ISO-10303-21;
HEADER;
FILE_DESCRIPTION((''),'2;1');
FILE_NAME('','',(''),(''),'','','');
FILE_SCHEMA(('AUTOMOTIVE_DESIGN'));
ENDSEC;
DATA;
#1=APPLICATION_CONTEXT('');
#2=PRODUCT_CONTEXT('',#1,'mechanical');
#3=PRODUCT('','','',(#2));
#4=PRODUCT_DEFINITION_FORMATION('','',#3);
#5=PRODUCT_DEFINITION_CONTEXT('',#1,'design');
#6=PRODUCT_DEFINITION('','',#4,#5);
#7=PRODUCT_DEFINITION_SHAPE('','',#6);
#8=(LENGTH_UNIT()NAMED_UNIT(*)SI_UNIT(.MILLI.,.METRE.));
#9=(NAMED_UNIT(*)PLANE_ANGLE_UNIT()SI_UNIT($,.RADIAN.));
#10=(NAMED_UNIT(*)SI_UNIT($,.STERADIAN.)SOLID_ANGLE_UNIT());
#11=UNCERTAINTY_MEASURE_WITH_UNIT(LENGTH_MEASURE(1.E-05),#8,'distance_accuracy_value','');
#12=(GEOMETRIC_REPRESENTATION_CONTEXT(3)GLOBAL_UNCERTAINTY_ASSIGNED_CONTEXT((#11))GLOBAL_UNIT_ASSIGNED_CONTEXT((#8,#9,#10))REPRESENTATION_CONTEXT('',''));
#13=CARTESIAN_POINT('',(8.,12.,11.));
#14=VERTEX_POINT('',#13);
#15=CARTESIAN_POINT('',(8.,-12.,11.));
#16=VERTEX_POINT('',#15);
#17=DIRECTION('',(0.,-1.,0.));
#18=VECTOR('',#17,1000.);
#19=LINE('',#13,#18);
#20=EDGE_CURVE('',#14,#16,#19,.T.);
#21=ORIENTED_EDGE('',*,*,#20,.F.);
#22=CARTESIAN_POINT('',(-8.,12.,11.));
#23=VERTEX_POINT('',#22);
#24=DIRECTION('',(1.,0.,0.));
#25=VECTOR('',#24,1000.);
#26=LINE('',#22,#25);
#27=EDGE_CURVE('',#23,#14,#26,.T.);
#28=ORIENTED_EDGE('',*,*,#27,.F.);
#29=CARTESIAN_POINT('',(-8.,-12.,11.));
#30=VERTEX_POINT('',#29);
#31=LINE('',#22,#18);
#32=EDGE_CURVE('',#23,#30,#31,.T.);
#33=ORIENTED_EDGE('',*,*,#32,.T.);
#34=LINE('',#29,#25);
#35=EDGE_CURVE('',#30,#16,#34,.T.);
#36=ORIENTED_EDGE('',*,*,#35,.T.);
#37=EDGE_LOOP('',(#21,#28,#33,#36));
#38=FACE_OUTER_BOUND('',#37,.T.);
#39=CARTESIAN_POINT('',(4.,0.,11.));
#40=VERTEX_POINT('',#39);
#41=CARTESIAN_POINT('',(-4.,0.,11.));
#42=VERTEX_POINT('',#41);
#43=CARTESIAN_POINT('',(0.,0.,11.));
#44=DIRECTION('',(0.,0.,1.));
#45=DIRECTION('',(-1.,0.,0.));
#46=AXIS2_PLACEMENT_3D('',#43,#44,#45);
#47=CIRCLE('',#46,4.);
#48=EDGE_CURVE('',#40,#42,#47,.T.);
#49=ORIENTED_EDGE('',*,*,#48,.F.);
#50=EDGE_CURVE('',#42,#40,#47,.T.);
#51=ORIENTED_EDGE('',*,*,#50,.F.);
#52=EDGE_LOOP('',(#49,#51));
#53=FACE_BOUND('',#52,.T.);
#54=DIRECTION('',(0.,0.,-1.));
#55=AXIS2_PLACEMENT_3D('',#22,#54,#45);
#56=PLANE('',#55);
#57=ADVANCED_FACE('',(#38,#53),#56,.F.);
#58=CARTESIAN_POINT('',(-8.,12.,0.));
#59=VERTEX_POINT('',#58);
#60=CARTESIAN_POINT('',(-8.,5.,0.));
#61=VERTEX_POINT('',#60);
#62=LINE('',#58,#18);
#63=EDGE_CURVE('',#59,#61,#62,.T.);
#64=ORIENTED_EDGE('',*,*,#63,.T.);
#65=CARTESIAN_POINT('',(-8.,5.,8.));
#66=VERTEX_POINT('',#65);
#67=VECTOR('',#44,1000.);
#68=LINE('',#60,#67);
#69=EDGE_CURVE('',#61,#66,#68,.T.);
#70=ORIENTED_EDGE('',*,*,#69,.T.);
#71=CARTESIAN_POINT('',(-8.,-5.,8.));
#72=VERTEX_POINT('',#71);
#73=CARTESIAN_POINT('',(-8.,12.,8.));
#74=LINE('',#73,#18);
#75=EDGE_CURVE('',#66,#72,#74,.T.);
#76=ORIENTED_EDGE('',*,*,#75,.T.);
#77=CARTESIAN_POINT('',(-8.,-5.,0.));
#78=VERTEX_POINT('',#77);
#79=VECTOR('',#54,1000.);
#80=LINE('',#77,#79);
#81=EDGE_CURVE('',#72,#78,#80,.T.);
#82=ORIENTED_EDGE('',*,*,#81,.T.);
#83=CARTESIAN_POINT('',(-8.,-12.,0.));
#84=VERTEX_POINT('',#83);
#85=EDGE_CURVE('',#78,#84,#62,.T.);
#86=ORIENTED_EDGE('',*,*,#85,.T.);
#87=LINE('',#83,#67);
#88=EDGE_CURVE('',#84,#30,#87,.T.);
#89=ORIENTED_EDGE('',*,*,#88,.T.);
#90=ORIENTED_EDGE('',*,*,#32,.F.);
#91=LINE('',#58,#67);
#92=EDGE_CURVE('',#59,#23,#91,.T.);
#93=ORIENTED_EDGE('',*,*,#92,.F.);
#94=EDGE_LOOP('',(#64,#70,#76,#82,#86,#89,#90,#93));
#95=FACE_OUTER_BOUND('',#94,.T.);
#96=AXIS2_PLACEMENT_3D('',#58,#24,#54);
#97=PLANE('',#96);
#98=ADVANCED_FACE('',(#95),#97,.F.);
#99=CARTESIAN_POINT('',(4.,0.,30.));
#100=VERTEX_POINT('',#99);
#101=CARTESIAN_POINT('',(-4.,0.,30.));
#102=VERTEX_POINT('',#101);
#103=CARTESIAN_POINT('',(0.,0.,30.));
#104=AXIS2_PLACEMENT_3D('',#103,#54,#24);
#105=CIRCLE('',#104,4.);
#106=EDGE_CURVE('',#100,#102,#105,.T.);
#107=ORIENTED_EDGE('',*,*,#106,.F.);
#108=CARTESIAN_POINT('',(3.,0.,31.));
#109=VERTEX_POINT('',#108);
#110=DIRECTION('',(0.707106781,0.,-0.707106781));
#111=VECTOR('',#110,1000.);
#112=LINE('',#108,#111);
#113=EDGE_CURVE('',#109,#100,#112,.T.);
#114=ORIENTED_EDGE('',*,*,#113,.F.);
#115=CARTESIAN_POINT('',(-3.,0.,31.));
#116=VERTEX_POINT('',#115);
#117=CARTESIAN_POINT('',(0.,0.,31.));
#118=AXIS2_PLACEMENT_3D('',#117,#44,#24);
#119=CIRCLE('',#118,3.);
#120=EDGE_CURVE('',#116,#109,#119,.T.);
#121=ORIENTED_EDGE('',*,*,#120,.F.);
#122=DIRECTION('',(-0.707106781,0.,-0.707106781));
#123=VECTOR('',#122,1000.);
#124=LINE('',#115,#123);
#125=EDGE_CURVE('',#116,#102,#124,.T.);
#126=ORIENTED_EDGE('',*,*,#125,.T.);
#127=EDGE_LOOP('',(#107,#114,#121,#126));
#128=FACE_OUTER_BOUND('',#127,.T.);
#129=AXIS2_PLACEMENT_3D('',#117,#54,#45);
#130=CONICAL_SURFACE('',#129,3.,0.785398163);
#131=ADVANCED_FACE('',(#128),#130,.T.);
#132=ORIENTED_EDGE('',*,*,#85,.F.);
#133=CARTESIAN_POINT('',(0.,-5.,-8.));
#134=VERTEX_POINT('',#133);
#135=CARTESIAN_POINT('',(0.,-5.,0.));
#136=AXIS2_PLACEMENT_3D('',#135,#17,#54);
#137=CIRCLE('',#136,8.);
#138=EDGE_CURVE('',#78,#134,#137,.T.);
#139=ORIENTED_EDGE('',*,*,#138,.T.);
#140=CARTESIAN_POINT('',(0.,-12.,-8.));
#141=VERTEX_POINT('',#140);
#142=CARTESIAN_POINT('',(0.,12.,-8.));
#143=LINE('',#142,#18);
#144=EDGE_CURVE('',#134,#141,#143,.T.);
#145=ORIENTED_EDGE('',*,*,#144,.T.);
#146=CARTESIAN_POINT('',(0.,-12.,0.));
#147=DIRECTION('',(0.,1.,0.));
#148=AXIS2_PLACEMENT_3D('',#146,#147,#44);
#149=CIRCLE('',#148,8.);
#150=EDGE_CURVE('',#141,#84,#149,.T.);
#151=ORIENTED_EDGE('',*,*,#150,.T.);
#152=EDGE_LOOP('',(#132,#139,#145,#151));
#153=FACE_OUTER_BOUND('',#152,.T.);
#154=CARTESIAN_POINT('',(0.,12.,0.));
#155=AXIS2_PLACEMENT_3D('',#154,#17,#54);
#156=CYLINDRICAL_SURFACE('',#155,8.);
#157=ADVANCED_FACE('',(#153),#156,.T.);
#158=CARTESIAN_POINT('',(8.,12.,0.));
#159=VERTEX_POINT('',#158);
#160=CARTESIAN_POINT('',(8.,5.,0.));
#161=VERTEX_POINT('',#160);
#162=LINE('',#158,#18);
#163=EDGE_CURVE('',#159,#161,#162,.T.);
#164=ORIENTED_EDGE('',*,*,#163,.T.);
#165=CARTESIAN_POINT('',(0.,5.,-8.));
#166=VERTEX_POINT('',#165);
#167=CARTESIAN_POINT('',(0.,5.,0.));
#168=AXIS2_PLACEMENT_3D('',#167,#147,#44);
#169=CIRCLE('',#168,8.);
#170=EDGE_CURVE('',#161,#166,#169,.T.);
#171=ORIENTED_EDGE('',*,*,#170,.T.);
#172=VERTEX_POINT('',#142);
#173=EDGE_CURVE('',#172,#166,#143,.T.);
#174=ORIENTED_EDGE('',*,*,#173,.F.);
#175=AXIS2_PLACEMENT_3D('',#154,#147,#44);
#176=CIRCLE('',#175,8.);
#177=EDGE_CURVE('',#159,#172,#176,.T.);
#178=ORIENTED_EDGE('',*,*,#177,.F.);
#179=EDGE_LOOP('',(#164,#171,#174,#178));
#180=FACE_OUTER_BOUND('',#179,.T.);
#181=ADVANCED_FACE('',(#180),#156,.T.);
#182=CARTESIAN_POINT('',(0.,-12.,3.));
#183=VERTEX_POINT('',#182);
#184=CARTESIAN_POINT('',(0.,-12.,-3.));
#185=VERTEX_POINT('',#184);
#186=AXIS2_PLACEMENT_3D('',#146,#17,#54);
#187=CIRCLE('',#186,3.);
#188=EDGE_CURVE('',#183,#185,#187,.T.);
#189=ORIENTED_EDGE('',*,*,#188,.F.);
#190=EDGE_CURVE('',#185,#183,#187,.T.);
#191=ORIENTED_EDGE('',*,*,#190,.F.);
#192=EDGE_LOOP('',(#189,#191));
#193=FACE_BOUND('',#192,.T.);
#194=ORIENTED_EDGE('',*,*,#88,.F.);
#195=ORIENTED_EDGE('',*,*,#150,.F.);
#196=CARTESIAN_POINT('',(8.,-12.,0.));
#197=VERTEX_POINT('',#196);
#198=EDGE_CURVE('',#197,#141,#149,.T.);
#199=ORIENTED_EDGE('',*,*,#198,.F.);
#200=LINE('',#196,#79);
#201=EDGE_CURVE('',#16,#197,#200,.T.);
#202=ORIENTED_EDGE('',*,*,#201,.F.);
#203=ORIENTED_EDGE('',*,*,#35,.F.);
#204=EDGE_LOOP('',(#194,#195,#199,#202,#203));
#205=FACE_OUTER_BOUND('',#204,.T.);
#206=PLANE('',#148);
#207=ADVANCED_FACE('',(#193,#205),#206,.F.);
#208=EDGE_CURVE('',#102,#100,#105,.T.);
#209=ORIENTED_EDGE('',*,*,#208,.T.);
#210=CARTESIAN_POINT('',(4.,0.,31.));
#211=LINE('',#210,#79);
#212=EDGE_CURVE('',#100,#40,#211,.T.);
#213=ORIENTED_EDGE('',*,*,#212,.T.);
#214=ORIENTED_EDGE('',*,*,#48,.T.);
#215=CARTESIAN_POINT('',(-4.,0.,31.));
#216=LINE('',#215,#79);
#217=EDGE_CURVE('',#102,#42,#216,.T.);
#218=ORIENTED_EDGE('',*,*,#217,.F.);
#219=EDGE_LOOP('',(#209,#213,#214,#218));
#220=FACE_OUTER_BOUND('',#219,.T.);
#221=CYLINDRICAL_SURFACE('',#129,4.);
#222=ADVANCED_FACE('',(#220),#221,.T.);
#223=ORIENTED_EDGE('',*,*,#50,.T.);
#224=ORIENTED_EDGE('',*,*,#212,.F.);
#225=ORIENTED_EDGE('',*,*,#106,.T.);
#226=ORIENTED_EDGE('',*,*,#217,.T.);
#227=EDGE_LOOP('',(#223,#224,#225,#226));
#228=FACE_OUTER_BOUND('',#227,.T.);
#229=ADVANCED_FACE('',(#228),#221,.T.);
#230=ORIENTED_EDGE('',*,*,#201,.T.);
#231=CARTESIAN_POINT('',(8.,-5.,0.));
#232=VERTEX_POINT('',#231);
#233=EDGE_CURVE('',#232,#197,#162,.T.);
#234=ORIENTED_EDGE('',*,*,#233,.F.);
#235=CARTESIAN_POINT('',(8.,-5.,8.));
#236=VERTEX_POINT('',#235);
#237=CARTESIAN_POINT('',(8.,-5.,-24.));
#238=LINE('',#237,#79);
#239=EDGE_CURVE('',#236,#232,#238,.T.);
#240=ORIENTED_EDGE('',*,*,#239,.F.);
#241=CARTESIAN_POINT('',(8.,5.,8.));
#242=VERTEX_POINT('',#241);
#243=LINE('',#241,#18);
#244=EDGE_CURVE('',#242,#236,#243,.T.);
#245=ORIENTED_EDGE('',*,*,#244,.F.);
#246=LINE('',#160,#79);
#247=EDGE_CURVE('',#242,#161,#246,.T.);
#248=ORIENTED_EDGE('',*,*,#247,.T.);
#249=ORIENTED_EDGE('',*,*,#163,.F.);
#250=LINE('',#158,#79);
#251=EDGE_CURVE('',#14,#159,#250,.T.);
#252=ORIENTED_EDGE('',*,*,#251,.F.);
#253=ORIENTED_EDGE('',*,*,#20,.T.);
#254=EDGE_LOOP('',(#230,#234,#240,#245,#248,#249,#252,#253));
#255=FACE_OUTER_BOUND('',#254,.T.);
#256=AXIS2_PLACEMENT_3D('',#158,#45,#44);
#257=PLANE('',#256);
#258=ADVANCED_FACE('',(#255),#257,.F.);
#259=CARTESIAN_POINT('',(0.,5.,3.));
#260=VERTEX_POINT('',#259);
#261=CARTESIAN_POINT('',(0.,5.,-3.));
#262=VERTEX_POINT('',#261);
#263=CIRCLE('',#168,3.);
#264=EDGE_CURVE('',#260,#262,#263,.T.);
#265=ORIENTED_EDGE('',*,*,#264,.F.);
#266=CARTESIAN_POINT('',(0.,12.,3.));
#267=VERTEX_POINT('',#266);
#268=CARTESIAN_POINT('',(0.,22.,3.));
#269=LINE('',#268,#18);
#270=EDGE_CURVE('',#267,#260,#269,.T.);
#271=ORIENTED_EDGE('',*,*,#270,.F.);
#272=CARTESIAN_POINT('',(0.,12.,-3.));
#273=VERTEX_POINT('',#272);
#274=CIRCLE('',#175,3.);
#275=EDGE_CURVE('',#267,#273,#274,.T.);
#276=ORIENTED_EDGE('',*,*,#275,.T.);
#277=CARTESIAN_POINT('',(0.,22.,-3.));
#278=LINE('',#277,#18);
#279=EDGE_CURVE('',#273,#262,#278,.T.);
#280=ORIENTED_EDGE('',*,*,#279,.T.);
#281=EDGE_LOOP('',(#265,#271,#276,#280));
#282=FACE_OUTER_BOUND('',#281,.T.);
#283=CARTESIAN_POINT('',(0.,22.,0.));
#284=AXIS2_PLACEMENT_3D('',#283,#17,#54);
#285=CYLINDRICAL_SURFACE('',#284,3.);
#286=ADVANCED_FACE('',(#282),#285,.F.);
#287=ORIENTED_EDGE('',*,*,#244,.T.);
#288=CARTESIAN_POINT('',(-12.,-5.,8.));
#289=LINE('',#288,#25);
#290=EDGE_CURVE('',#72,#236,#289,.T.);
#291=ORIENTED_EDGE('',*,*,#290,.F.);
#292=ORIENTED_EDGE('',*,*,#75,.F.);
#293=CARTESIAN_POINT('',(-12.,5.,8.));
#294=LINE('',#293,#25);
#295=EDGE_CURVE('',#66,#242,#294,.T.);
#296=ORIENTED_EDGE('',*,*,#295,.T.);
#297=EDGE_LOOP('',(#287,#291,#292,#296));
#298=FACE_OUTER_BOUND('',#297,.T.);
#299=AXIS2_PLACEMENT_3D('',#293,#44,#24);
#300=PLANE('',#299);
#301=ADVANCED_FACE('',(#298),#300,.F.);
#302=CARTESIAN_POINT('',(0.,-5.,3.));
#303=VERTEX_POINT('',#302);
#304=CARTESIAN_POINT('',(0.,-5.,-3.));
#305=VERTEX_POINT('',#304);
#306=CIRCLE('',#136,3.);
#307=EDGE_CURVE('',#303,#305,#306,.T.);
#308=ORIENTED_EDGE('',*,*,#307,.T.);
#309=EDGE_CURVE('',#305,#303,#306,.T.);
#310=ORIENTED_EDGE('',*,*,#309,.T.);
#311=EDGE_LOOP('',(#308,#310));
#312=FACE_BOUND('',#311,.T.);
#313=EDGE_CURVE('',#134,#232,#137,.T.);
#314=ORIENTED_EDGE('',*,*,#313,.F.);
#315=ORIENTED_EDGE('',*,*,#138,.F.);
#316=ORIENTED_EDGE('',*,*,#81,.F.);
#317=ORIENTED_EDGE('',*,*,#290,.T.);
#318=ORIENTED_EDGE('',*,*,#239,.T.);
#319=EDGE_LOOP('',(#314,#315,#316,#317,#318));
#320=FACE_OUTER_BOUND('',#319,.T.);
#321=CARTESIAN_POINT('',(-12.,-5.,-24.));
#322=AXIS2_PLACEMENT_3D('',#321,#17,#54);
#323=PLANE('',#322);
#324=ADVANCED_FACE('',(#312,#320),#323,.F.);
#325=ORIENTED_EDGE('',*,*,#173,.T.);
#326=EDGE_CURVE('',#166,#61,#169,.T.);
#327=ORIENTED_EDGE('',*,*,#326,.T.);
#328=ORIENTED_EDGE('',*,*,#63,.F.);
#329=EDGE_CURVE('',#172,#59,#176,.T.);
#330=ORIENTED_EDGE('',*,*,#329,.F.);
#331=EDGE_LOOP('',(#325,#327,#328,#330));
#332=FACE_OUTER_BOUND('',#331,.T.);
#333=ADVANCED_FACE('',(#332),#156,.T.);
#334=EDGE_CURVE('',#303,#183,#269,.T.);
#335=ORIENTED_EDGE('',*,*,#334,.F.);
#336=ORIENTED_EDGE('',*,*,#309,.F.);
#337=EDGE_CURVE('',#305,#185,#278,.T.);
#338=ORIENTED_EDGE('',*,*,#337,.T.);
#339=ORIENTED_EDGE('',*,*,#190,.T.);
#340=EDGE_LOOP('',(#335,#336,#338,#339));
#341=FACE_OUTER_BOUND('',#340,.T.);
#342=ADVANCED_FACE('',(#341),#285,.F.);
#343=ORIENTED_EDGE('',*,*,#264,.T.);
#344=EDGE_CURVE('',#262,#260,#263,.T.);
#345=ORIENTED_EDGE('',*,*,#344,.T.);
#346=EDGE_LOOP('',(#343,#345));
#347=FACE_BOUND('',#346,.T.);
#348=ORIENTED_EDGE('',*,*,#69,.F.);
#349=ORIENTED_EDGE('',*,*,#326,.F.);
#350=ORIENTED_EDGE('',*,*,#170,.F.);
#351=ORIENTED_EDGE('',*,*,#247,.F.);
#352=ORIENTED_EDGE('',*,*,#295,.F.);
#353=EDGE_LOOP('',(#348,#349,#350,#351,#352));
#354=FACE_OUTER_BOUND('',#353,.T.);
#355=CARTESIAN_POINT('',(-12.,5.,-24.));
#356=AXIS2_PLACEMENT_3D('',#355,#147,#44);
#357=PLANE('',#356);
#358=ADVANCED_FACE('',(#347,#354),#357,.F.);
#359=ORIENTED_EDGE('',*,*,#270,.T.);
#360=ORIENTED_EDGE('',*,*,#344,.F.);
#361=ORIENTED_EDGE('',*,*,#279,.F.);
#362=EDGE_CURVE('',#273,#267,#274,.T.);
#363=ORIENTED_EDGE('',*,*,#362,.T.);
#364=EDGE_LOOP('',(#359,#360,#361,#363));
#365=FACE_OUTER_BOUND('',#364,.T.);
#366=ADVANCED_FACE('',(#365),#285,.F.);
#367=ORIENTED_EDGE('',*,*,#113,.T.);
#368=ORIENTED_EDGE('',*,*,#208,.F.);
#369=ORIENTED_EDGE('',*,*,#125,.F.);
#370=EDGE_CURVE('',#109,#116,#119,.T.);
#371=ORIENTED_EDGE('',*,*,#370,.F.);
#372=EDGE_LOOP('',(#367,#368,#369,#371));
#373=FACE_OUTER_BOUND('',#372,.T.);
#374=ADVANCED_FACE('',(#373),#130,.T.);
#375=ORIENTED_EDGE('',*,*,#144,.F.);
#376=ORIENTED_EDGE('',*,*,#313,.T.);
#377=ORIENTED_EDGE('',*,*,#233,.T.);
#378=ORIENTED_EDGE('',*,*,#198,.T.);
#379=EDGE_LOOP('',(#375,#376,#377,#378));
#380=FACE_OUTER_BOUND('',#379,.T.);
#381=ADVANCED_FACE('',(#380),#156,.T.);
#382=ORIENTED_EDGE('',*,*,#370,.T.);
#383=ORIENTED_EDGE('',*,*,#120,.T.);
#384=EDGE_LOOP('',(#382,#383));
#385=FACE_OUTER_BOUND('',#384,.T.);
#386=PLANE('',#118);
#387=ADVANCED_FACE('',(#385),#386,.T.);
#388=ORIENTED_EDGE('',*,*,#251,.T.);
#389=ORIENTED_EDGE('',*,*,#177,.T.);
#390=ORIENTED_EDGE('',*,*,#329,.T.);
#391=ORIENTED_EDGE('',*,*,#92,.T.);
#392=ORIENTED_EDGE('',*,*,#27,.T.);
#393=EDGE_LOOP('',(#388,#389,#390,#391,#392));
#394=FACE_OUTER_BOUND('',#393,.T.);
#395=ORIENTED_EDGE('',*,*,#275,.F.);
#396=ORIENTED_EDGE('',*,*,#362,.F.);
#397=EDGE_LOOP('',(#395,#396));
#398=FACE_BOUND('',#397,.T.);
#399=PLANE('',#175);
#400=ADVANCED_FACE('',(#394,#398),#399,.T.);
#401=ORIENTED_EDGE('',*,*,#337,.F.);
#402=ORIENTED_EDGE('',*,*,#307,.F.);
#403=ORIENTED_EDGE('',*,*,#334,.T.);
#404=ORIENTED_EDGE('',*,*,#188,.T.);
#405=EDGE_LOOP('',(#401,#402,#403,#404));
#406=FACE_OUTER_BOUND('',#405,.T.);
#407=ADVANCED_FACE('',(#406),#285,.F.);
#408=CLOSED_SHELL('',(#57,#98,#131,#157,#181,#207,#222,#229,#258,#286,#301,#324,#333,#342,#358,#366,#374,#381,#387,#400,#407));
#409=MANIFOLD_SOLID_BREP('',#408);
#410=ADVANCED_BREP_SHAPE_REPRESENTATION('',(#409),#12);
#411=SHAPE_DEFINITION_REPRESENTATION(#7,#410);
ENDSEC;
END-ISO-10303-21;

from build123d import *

# Parameters (mm, degrees)
BOSS_EXTRUDE1_DEPTH = 12
SKETCH2_R           = 4
BOSS_EXTRUDE2_DEPTH = 20
SKETCH3_W           = 32
SKETCH3_H           = 10
CUT_EXTRUDE1_DEPTH  = 20
SKETCH4_R           = 3
CUT_EXTRUDE2_DEPTH  = 34
CHAMFER1_SIZE       = 1


with BuildPart() as part:
    # Sketch1 → Boss-Extrude1 (new, symmetric)
    with BuildSketch(Plane(origin=(0, 0, 0), x_dir=(1, 0, 0), z_dir=(0, 1, 0))):
        with BuildLine():
            Line((-8, 0), (-8, -11))
            Line((-8, -11), (8, -11))
            Line((8, -11), (8, 0))
            ThreePointArc((8, 0), (0, 8), (-8, 0))
        make_face()
    extrude(amount=BOSS_EXTRUDE1_DEPTH, both=True)

    # Sketch2 → Boss-Extrude2 (add)
    with BuildSketch(Plane.XY.offset(11)):
        with Locations(Location((0, 0, 0), (0, 0, 180))):
            Circle(SKETCH2_R)
    extrude(amount=BOSS_EXTRUDE2_DEPTH)

    # Sketch3 → Cut-Extrude1 (cut)
    with BuildSketch(Plane(origin=(8, 0, 0), x_dir=(0, 0, -1), z_dir=(1, 0, 0))):
        with Locations((8, 0)):
            Rectangle(SKETCH3_W, SKETCH3_H)
    extrude(amount=-CUT_EXTRUDE1_DEPTH, mode=Mode.SUBTRACT)

    # Sketch4 → Cut-Extrude2 (cut)
    with BuildSketch(Plane.XZ.offset(12)):
        with Locations(Location((0, 0, 0), (0, 0, 270))):
            Circle(SKETCH4_R)
    extrude(amount=-CUT_EXTRUDE2_DEPTH, mode=Mode.SUBTRACT)

    # Chamfer1
    chamfer1_edges = [part.edges().sort_by_distance(p)[0] for p in [
        (4, 0, 31),
    ]]
    chamfer(chamfer1_edges, length=CHAMFER1_SIZE)


solid = part.part
